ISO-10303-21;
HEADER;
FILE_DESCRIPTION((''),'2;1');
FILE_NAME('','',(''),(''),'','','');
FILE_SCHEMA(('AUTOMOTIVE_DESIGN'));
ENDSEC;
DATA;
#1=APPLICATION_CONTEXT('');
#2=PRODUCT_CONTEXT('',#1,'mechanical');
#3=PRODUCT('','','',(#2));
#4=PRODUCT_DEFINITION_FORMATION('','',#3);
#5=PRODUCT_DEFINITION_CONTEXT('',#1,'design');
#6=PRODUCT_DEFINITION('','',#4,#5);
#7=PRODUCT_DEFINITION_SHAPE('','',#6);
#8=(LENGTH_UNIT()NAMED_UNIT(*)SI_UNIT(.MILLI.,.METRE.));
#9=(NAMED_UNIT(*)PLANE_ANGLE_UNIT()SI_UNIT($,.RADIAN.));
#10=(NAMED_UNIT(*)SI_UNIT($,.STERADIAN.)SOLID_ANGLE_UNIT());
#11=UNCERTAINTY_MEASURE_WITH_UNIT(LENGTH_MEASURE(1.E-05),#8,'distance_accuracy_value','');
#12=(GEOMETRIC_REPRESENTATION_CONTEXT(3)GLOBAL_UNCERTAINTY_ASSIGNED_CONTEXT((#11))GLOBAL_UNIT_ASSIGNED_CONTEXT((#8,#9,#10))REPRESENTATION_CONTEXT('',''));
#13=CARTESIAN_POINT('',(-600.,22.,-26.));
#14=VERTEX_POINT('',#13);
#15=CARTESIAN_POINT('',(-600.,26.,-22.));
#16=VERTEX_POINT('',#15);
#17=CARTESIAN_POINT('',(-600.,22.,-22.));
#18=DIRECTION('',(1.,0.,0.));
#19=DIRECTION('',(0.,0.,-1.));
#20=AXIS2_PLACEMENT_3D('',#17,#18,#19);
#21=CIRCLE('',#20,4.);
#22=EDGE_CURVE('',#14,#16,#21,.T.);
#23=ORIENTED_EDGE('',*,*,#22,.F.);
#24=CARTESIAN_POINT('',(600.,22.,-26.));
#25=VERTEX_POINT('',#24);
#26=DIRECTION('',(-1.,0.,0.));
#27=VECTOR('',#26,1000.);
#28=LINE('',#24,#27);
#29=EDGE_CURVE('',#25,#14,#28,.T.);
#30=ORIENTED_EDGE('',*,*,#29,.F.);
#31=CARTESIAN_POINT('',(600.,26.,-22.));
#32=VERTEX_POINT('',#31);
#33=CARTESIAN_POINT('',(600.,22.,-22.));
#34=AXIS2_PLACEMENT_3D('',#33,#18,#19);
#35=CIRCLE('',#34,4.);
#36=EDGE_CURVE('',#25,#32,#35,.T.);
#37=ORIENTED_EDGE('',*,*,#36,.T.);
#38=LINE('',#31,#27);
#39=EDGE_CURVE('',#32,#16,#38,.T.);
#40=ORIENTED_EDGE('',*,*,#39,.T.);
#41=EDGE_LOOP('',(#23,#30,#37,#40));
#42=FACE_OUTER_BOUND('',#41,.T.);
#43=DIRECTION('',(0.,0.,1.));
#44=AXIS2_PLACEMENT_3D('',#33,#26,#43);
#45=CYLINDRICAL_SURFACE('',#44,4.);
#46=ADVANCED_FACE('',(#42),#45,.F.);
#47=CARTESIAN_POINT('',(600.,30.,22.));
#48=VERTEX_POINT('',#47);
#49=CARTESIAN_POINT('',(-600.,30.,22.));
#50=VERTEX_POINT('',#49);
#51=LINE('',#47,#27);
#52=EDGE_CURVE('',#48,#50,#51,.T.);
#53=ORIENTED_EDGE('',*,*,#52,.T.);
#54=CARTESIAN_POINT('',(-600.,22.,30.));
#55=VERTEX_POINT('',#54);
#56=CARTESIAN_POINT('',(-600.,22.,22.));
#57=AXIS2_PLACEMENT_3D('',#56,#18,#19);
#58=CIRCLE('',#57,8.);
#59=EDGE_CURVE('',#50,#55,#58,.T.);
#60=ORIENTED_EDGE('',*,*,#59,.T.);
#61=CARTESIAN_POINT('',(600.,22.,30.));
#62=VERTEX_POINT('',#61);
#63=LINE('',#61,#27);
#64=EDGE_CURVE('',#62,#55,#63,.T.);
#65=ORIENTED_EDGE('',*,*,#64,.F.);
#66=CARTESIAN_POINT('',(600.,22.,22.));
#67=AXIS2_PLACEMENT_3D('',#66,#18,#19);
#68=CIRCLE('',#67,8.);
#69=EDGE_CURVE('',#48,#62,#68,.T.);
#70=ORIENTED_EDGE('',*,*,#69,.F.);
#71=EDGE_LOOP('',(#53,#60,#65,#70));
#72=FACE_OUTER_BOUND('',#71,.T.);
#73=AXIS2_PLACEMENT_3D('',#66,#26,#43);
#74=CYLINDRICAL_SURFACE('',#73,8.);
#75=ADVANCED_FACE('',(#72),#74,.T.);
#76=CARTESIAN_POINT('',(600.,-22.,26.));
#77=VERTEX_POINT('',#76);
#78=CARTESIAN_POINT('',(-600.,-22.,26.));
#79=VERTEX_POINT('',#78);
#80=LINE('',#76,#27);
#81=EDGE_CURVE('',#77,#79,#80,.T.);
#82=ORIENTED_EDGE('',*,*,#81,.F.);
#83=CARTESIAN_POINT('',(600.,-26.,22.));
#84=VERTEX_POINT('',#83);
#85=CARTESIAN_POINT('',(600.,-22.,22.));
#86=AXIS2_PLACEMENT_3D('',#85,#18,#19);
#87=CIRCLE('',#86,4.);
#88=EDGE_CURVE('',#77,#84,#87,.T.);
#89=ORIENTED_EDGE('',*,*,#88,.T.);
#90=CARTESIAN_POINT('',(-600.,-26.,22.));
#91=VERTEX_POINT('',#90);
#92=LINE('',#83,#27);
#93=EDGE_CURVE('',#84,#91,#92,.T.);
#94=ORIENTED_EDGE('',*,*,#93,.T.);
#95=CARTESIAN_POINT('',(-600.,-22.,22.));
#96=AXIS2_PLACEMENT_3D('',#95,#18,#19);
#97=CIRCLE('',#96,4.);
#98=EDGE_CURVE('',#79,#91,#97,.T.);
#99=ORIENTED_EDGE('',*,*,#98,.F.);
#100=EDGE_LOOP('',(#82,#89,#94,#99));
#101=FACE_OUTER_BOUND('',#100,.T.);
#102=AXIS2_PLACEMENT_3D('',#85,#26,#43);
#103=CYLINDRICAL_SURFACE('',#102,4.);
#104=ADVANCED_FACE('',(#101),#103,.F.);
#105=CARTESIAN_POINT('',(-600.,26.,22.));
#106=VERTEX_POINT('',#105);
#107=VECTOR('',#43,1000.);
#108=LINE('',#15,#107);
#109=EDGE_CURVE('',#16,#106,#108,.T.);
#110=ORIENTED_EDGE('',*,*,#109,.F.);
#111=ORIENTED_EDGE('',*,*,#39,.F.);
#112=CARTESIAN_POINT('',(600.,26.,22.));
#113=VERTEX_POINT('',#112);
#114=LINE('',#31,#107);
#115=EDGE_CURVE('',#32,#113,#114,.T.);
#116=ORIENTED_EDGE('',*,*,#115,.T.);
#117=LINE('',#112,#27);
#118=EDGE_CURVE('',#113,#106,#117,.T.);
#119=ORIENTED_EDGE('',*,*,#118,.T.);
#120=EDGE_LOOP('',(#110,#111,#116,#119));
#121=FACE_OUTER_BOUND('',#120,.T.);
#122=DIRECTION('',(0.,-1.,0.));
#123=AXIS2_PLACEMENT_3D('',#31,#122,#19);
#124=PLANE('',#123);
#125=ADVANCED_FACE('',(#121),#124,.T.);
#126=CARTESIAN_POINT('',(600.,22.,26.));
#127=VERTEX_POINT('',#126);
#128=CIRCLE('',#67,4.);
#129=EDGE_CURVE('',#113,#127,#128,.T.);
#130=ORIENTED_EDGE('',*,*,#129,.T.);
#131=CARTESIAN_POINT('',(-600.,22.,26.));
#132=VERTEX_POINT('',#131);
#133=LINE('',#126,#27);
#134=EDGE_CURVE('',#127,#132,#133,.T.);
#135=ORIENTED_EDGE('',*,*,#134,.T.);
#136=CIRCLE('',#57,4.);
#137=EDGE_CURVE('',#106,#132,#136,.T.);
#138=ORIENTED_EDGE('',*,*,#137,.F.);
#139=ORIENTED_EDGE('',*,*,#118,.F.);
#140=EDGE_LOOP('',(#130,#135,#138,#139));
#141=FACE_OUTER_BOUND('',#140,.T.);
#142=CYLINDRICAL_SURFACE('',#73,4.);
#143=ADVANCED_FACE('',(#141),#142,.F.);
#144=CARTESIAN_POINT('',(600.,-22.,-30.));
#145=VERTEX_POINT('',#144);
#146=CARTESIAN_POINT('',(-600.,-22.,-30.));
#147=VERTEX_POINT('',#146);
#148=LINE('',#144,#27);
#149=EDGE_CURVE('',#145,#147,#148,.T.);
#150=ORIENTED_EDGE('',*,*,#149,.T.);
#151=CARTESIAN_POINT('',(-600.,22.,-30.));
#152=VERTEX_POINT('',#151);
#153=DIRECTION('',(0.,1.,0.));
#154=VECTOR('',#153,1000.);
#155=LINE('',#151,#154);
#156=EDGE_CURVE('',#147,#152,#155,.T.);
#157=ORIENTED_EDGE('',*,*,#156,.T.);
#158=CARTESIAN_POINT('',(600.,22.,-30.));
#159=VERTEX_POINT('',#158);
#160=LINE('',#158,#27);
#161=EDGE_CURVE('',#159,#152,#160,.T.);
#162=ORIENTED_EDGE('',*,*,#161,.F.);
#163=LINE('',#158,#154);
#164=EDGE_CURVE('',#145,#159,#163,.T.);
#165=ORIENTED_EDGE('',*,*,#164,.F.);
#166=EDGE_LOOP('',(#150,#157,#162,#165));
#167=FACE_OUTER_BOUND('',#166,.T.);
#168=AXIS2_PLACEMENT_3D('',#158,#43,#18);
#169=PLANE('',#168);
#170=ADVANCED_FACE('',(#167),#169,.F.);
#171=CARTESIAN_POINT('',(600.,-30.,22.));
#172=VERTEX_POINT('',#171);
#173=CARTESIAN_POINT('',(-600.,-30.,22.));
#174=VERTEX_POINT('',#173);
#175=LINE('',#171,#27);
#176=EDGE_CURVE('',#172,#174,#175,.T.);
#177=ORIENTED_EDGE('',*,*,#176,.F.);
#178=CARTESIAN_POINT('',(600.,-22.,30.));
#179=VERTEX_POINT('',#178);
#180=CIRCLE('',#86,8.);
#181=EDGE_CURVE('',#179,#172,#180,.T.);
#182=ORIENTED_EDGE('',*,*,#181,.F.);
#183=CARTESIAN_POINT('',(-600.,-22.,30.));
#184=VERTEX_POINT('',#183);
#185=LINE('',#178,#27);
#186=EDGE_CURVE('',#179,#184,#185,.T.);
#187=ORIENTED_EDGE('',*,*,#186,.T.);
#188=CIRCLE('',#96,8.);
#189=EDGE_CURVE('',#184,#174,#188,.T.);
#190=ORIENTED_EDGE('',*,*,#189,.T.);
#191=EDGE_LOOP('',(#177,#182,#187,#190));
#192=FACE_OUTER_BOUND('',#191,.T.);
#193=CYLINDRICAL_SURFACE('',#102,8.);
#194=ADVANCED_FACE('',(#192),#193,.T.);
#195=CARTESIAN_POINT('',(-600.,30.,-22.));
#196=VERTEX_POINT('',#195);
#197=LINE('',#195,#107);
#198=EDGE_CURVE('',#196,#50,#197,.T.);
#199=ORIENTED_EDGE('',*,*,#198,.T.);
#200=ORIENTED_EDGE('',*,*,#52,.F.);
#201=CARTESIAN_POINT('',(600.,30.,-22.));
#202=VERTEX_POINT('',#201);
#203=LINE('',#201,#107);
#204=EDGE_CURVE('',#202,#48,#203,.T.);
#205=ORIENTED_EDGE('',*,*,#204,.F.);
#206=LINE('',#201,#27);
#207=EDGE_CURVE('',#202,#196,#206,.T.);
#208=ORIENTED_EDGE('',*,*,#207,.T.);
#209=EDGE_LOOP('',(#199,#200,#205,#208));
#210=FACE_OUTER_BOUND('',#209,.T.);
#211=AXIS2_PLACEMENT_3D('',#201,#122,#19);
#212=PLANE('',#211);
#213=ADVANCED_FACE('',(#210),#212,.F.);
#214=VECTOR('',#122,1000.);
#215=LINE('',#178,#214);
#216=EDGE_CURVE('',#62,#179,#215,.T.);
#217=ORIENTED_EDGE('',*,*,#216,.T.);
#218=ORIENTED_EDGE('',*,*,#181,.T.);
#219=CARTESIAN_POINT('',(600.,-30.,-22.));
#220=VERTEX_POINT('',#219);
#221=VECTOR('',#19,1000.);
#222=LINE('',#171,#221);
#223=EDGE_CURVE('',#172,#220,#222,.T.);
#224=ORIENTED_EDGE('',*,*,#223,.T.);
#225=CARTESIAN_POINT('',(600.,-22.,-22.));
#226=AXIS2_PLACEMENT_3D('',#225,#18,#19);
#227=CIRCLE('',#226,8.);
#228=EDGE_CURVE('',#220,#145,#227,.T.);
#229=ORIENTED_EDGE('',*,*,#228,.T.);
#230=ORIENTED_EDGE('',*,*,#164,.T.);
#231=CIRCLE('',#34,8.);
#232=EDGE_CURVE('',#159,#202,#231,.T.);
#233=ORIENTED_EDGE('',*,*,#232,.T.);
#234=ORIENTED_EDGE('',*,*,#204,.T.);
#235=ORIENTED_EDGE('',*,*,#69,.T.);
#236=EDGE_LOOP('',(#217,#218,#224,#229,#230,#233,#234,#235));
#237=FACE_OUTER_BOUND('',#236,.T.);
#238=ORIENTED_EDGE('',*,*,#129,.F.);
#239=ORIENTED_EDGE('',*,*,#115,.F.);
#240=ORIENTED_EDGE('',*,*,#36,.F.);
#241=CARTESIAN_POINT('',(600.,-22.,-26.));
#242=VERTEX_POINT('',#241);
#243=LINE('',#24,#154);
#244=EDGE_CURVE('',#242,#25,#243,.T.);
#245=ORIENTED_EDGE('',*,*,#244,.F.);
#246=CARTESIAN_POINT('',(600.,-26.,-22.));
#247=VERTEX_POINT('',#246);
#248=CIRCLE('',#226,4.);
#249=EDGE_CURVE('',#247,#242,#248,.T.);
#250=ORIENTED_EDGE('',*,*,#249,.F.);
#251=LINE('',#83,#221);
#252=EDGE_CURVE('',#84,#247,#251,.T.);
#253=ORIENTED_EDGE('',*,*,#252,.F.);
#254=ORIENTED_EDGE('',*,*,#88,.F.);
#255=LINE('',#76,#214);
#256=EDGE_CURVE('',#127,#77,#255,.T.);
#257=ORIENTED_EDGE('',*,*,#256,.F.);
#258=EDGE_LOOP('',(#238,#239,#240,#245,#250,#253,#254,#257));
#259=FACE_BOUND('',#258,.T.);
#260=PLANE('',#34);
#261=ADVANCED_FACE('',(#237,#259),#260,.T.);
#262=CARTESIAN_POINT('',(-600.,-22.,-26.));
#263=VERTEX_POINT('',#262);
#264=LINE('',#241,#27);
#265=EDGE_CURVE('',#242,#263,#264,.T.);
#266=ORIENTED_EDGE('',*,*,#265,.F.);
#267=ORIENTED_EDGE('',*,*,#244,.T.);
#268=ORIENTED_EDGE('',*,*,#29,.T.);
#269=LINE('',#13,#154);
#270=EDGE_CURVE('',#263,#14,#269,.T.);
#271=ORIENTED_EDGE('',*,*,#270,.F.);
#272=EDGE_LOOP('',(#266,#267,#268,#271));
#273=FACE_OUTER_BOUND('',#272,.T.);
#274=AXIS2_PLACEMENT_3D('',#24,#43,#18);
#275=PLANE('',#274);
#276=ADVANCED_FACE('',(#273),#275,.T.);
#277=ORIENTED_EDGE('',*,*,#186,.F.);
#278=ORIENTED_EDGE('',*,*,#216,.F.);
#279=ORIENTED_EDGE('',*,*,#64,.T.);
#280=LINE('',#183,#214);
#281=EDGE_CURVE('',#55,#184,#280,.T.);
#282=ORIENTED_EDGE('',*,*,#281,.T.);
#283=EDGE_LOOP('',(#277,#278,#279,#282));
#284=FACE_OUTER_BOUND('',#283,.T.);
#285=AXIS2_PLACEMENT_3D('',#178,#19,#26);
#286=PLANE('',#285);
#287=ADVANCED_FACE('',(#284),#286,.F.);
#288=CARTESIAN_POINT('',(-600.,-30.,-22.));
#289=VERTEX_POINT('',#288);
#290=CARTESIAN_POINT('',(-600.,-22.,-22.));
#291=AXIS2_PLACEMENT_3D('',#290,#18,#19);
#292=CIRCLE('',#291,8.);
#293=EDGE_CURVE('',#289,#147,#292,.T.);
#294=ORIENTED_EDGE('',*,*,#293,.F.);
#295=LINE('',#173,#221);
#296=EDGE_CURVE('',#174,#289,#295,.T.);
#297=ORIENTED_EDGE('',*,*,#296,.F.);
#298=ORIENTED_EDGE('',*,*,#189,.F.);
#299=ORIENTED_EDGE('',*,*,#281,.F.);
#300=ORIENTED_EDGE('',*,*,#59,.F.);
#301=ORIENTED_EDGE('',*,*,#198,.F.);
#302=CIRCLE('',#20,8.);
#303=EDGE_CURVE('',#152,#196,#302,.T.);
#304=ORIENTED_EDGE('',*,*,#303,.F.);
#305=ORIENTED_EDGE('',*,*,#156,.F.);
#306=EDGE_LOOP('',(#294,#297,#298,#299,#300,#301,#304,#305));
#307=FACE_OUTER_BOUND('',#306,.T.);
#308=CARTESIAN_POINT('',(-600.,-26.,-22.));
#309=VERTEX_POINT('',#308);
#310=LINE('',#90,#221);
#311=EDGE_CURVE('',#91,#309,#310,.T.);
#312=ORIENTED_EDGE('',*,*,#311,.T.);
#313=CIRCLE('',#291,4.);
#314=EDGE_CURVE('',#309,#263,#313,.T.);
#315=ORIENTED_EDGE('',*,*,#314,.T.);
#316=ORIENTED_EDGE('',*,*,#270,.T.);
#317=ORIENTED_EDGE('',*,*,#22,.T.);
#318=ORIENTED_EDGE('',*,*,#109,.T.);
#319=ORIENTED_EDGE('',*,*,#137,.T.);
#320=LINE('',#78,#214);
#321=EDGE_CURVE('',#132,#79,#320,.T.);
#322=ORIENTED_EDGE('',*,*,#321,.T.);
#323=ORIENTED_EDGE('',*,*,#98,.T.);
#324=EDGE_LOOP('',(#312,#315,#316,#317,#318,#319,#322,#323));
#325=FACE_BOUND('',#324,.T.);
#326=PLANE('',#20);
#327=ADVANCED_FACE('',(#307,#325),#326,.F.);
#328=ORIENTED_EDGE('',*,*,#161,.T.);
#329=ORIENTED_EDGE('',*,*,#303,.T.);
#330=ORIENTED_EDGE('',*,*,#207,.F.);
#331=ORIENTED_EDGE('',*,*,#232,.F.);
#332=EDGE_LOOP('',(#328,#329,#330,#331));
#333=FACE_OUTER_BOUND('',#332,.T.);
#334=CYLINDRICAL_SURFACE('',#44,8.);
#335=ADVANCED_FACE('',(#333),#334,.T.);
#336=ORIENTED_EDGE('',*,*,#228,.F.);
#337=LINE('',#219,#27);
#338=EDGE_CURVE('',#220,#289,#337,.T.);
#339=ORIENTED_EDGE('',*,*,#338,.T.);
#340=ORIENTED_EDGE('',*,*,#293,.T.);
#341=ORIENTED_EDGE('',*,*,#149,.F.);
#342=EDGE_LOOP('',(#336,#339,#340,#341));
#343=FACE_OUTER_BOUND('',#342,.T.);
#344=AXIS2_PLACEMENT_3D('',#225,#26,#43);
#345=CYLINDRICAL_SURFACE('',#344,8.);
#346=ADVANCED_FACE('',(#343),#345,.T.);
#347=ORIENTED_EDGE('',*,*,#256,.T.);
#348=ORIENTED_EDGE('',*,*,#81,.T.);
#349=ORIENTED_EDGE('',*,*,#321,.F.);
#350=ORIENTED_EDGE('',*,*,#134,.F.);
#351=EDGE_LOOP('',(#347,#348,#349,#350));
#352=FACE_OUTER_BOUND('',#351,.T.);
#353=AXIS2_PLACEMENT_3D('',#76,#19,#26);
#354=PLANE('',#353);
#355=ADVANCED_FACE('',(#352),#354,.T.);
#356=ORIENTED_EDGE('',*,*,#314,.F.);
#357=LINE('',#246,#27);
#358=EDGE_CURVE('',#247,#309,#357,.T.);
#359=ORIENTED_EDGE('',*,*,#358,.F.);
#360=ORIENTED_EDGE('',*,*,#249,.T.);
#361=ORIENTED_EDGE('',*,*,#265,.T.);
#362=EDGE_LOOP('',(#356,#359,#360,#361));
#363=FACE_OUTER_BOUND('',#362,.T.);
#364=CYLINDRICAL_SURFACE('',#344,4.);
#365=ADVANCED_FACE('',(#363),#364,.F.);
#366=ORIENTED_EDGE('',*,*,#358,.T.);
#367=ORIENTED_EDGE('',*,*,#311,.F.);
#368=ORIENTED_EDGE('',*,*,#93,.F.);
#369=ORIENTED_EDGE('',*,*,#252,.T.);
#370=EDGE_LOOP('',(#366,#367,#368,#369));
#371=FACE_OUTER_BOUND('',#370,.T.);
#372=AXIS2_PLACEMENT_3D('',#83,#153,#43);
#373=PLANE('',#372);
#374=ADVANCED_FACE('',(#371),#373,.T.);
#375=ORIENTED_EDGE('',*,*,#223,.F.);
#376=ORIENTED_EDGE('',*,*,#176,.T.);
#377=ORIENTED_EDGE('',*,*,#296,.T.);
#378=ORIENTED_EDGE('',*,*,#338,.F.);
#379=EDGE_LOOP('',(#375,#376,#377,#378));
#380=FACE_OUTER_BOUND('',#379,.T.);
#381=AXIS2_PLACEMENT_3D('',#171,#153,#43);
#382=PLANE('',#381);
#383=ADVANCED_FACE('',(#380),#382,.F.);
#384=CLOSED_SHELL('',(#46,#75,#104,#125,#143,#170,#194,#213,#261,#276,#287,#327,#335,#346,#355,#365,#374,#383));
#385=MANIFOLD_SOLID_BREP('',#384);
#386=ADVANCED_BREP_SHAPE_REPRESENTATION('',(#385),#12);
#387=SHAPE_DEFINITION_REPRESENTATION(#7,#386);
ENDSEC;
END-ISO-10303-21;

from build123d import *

# Parameters (mm, degrees)
GB_6728_1986_60_X_60_X_4_1_DEPTH = 1200


with BuildPart() as part:
    # Sketch11 → Gb／6728-1986方形空心型钢 60 X 60 X 4(1) (new body)
    with BuildSketch(Plane(origin=(-600, 0, 0), x_dir=(0, 0, -1), z_dir=(1, 0, 0))):
        with BuildLine():
            Line((-22, -30), (22, -30))
            ThreePointArc((22, -30), (27.656854249, -27.656854249), (30, -22))
            Line((30, -22), (30, 22))
            ThreePointArc((30, 22), (27.656854249, 27.656854249), (22, 30))
            Line((22, 30), (-22, 30))
            ThreePointArc((-22, 30), (-27.656854249, 27.656854249), (-30, 22))
            Line((-30, 22), (-30, -22))
            ThreePointArc((-30, -22), (-27.656854249, -27.656854249), (-22, -30))
        make_face()
        with BuildLine():
            Line((-22, -26), (22, -26))
            ThreePointArc((22, -26), (24.828427125, -24.828427125), (26, -22))
            Line((26, -22), (26, 22))
            ThreePointArc((26, 22), (24.828427125, 24.828427125), (22, 26))
            Line((22, 26), (-22, 26))
            ThreePointArc((-22, 26), (-24.828427125, 24.828427125), (-26, 22))
            Line((-26, 22), (-26, -22))
            ThreePointArc((-26, -22), (-24.828427125, -24.828427125), (-22, -26))
        make_face(mode=Mode.SUBTRACT)
    extrude(amount=GB_6728_1986_60_X_60_X_4_1_DEPTH)


solid = part.part
